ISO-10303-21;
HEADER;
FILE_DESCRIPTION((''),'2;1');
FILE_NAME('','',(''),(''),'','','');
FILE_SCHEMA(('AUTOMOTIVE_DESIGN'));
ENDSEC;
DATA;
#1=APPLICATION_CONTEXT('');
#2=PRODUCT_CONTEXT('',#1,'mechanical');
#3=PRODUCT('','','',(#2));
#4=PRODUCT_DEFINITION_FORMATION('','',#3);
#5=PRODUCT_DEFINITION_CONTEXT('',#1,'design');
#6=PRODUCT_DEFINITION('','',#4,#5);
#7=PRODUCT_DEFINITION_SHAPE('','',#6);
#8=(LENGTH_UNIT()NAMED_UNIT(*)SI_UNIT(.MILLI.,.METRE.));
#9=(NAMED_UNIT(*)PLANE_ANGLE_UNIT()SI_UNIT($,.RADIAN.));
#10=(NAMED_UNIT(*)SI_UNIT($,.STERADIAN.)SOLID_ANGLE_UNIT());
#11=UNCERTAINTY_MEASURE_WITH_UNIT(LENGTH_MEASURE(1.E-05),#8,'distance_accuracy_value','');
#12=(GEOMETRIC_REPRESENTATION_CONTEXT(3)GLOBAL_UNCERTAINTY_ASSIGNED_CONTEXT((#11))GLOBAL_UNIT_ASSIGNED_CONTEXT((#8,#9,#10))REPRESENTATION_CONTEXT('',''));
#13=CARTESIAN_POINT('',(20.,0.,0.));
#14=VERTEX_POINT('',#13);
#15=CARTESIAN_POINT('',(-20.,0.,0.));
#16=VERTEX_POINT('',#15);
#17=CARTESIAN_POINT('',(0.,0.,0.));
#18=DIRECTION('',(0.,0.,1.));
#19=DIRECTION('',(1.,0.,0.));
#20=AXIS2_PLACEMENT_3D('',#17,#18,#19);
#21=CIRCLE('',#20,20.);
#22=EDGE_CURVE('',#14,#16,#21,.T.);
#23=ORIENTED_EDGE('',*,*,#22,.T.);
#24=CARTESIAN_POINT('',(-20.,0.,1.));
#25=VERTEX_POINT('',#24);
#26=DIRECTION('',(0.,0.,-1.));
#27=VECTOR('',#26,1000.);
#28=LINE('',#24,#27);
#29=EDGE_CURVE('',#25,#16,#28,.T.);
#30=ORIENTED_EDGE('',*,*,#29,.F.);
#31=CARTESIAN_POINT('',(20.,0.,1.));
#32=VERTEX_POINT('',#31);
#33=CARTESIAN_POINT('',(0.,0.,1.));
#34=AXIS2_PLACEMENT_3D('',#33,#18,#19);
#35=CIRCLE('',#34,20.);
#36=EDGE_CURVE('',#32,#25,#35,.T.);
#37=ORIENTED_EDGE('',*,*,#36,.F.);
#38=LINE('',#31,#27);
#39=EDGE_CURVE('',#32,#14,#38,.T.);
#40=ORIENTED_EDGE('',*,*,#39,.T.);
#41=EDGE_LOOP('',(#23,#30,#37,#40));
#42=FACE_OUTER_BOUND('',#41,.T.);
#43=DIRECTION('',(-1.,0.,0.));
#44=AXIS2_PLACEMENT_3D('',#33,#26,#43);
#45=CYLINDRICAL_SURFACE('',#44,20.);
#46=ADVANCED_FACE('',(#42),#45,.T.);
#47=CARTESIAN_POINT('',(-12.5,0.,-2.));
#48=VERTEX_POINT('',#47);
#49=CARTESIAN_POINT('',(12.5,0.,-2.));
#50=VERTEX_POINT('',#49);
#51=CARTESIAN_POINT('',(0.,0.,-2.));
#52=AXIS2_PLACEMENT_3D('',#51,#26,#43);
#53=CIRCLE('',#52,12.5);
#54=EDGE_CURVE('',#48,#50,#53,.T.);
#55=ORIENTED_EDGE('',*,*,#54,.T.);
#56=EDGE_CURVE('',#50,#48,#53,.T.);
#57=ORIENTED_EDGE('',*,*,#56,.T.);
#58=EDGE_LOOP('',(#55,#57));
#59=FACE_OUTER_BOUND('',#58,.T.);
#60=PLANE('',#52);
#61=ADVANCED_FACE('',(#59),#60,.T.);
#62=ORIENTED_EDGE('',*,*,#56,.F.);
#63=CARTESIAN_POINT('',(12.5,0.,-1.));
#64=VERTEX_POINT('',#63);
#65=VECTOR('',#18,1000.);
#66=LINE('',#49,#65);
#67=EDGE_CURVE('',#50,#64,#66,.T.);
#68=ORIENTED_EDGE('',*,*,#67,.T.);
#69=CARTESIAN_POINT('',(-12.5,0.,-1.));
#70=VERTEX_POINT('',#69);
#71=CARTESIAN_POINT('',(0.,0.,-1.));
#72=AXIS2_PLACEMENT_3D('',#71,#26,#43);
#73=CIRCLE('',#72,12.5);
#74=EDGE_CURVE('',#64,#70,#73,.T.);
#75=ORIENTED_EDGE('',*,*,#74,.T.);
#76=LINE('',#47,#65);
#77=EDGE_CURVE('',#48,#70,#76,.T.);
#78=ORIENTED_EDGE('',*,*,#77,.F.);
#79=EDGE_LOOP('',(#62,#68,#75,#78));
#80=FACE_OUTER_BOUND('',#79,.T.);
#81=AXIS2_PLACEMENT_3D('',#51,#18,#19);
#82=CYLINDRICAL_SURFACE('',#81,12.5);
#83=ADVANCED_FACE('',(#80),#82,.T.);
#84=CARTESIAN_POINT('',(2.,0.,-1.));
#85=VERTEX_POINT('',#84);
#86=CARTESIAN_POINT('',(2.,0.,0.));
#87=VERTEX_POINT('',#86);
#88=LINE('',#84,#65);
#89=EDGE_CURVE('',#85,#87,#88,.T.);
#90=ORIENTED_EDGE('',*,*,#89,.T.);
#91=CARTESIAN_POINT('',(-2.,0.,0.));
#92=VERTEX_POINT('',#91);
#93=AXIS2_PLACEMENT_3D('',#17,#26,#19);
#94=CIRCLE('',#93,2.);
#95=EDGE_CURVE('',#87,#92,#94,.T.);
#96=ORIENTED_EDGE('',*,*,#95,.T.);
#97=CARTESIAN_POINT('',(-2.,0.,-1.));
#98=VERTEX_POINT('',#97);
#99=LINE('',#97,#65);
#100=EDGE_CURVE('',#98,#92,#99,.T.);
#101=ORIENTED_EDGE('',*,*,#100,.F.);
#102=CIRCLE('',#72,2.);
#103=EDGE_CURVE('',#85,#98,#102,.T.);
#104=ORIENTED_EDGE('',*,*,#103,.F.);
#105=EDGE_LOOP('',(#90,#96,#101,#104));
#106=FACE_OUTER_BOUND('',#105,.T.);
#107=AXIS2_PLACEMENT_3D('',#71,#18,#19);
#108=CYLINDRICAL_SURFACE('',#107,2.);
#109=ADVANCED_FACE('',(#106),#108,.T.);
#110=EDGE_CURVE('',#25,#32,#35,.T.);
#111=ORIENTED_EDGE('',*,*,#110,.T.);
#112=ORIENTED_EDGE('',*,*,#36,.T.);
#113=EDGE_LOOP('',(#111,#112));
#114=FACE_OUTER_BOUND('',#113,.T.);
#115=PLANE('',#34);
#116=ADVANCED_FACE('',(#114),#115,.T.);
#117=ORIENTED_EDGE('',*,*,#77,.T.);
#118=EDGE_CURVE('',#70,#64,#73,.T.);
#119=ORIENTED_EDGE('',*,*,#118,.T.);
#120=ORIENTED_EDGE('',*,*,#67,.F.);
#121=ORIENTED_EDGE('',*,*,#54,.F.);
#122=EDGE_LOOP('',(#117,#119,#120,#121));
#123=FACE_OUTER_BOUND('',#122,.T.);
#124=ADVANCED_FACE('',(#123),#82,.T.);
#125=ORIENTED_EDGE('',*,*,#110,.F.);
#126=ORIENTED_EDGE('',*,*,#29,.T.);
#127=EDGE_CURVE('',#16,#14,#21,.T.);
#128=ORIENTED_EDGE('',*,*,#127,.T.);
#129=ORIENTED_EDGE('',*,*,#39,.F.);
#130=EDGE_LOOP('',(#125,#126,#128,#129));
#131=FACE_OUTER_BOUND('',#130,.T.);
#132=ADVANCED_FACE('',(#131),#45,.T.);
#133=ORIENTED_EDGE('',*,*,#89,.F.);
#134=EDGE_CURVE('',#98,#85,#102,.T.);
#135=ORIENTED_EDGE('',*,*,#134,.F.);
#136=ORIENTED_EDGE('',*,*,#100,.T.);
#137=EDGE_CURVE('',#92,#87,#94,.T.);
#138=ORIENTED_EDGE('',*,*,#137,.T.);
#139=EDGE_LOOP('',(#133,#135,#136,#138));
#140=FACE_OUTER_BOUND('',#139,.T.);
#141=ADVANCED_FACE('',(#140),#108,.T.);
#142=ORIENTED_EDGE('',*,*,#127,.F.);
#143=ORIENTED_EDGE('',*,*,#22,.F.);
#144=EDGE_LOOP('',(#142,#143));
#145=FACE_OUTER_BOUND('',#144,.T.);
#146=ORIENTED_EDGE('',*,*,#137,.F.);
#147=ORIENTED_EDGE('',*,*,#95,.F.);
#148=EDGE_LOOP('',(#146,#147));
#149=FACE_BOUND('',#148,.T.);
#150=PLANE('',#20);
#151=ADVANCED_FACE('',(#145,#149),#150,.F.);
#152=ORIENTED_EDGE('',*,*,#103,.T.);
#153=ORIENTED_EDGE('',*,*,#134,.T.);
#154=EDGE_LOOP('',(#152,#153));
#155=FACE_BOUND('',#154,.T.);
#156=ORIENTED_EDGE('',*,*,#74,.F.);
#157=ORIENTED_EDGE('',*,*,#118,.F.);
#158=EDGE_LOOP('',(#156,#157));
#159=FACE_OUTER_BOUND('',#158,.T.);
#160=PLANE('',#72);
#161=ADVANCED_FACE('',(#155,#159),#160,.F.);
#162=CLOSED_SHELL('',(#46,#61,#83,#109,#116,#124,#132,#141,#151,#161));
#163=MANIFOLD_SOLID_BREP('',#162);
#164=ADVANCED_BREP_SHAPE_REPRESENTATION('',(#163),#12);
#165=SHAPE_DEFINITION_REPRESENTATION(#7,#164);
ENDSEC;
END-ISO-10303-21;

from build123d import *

# Parameters (mm, degrees)
SKETCH1_R           = 20
BOSS_EXTRUDE1_DEPTH = 1
SKETCH2_R           = 2
BOSS_EXTRUDE2_DEPTH = 1
SKETCH3_R           = 12.5
BOSS_EXTRUDE3_DEPTH = 1


with BuildPart() as part:
    # Sketch1 → Boss-Extrude1 (new body)
    with BuildSketch(Plane.XY):
        Circle(SKETCH1_R)
    extrude(amount=BOSS_EXTRUDE1_DEPTH)

    # Sketch2 → Boss-Extrude2 (add)
    with BuildSketch(Plane(origin=(0, 0, 0), x_dir=(-1, 0, 0), z_dir=(0, 0, -1))):
        with Locations(Location((0, 0, 0), (0, 0, 180))):
            Circle(SKETCH2_R)
    extrude(amount=BOSS_EXTRUDE2_DEPTH)

    # Sketch3 → Boss-Extrude3 (add)
    with BuildSketch(Plane(origin=(0, 0, -1), x_dir=(-1, 0, 0), z_dir=(0, 0, -1))):
        Circle(SKETCH3_R)
    extrude(amount=BOSS_EXTRUDE3_DEPTH)


solid = part.part
